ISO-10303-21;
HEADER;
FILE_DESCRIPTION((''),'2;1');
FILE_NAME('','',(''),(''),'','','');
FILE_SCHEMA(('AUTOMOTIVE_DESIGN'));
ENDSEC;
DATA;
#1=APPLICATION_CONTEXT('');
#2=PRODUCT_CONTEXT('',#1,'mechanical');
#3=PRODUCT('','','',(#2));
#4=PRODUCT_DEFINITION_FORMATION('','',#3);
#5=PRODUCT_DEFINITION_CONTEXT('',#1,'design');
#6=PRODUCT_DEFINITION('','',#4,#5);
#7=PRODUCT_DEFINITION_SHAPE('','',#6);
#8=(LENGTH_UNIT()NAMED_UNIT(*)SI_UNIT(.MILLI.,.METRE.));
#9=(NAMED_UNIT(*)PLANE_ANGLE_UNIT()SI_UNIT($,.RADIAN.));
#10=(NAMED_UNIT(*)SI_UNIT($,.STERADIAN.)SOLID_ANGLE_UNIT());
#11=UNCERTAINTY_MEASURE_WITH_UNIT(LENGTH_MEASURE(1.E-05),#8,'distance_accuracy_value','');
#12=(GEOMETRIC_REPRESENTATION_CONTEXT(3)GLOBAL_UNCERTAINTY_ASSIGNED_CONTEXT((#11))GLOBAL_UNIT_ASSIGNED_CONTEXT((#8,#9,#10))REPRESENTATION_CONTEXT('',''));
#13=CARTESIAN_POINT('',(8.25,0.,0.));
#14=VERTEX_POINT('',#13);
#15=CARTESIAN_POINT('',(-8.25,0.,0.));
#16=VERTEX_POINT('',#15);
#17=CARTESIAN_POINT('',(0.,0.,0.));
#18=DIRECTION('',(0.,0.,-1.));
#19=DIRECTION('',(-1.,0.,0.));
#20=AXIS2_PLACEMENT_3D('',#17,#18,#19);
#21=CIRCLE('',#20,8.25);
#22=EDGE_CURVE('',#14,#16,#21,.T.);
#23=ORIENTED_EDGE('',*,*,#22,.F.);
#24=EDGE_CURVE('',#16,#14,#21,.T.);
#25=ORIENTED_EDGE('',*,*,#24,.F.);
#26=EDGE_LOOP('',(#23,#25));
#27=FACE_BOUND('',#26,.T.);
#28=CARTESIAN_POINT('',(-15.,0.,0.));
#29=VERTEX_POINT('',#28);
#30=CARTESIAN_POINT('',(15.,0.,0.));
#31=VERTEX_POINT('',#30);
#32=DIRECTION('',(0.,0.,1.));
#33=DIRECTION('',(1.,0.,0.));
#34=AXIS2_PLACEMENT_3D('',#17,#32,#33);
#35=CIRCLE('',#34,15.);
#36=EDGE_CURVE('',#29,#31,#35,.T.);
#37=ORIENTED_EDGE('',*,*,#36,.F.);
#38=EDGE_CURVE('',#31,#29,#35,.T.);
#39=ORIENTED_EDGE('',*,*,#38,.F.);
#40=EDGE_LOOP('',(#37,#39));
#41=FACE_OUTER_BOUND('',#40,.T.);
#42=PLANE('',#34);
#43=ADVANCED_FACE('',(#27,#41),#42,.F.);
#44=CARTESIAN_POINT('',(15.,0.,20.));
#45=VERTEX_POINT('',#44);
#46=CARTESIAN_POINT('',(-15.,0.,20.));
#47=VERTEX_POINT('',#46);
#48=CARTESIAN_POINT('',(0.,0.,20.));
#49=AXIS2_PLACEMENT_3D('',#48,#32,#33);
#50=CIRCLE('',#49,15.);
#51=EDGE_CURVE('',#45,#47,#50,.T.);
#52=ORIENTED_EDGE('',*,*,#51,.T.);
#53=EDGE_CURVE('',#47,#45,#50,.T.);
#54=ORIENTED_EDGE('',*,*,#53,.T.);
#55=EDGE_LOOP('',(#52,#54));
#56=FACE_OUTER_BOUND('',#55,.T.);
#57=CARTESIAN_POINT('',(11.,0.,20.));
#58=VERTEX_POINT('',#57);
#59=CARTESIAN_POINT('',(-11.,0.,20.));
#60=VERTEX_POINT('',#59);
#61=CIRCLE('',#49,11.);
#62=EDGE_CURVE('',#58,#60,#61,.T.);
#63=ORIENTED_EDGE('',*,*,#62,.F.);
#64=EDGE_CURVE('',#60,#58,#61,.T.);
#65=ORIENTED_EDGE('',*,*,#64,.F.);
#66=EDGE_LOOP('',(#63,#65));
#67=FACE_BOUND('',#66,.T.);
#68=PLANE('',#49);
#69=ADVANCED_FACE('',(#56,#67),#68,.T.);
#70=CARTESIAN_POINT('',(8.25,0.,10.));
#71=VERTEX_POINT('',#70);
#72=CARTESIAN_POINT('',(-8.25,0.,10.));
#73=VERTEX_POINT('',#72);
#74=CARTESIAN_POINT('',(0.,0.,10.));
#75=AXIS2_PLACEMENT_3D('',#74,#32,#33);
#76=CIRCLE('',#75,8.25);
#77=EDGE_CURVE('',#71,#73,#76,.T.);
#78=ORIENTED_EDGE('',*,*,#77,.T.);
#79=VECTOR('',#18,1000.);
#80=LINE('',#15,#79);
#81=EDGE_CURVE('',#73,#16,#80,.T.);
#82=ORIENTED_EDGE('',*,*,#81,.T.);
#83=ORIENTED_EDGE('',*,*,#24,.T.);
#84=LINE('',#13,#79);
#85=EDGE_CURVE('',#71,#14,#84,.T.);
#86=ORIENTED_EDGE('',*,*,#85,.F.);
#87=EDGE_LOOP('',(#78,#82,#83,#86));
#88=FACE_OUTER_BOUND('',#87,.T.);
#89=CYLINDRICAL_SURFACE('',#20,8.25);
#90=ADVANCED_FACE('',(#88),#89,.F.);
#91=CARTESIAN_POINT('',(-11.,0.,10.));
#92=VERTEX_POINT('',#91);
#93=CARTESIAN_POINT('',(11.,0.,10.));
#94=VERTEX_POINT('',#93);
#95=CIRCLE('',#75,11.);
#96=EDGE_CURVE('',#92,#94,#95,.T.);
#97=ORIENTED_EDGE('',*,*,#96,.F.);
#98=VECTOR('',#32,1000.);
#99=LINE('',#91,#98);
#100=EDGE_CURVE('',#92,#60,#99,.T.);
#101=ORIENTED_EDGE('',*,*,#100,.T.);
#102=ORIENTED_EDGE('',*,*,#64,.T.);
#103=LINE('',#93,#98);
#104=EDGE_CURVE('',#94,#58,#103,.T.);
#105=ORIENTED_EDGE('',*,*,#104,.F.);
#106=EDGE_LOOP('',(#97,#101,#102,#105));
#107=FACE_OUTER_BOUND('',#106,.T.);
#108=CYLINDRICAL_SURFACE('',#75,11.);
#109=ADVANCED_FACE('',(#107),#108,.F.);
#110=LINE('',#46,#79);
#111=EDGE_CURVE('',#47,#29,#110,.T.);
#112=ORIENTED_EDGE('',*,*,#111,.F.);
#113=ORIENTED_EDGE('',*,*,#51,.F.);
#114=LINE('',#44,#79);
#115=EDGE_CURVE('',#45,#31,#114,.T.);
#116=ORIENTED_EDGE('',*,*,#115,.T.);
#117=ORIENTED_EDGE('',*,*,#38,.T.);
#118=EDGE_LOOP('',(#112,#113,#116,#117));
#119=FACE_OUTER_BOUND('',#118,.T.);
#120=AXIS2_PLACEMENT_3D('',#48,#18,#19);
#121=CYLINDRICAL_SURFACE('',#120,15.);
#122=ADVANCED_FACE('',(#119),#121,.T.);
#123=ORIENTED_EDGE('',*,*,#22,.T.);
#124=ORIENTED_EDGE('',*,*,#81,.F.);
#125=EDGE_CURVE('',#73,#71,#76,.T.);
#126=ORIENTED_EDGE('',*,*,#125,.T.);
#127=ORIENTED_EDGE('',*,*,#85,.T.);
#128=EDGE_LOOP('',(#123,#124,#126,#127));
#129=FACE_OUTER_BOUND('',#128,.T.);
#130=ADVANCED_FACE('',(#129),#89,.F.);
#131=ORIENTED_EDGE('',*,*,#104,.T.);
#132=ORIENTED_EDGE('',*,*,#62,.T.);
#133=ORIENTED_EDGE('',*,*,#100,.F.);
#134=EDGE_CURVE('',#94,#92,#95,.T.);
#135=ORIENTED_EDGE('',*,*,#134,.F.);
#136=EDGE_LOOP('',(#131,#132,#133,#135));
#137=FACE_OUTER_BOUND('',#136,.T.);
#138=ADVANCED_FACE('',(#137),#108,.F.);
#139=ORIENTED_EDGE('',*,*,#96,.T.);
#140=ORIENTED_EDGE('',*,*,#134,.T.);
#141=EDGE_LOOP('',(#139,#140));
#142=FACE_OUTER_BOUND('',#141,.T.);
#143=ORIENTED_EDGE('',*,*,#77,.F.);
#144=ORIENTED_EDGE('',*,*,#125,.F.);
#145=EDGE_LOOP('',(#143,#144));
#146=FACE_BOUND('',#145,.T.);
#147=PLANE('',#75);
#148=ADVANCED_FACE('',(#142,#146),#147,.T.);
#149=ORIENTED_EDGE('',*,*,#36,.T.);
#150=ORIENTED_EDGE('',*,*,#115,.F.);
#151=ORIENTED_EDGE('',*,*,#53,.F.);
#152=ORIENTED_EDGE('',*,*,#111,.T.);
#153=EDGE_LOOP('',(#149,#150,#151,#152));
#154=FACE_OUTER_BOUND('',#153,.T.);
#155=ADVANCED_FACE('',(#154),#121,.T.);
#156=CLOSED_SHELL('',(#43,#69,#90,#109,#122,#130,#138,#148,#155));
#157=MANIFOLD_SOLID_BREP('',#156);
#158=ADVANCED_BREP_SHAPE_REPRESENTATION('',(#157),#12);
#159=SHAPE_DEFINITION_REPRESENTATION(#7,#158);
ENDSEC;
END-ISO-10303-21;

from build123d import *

# Parameters (mm, degrees)
SKETCH1_R                  = 15
BOSS_EXTRUDE1_DEPTH        = 20
SKETCH2_R                  = 11
CUT_EXTRUDE1_DEPTH         = 10
M18X1_5_TAPPED_HOLE1_D     = 16.5
M18X1_5_TAPPED_HOLE1_DEPTH = 40.5
M18X1_5_TAPPED_HOLE1_TIP   = 4.957100107


with BuildPart() as part:
    # Sketch1 → Boss-Extrude1 (new body)
    with BuildSketch(Plane.XY):
        Circle(SKETCH1_R)
    extrude(amount=BOSS_EXTRUDE1_DEPTH)

    # Sketch2 → Cut-Extrude1 (cut)
    with BuildSketch(Plane.XY.offset(20)):
        Circle(SKETCH2_R)
    extrude(amount=-CUT_EXTRUDE1_DEPTH, mode=Mode.SUBTRACT)

    # M18x1.5 Tapped Hole1
    with Locations(Plane(origin=(0, 0, 0), x_dir=(-1, 0, 0), z_dir=(0, 0, -1))):
        with Locations((0, 0)):
            Hole(M18X1_5_TAPPED_HOLE1_D / 2, depth=M18X1_5_TAPPED_HOLE1_DEPTH)
            with Locations((0, 0, -(M18X1_5_TAPPED_HOLE1_DEPTH + M18X1_5_TAPPED_HOLE1_TIP / 2))):  # 118° drill point
                Cone(0, M18X1_5_TAPPED_HOLE1_D / 2, M18X1_5_TAPPED_HOLE1_TIP, mode=Mode.SUBTRACT)


solid = part.part
